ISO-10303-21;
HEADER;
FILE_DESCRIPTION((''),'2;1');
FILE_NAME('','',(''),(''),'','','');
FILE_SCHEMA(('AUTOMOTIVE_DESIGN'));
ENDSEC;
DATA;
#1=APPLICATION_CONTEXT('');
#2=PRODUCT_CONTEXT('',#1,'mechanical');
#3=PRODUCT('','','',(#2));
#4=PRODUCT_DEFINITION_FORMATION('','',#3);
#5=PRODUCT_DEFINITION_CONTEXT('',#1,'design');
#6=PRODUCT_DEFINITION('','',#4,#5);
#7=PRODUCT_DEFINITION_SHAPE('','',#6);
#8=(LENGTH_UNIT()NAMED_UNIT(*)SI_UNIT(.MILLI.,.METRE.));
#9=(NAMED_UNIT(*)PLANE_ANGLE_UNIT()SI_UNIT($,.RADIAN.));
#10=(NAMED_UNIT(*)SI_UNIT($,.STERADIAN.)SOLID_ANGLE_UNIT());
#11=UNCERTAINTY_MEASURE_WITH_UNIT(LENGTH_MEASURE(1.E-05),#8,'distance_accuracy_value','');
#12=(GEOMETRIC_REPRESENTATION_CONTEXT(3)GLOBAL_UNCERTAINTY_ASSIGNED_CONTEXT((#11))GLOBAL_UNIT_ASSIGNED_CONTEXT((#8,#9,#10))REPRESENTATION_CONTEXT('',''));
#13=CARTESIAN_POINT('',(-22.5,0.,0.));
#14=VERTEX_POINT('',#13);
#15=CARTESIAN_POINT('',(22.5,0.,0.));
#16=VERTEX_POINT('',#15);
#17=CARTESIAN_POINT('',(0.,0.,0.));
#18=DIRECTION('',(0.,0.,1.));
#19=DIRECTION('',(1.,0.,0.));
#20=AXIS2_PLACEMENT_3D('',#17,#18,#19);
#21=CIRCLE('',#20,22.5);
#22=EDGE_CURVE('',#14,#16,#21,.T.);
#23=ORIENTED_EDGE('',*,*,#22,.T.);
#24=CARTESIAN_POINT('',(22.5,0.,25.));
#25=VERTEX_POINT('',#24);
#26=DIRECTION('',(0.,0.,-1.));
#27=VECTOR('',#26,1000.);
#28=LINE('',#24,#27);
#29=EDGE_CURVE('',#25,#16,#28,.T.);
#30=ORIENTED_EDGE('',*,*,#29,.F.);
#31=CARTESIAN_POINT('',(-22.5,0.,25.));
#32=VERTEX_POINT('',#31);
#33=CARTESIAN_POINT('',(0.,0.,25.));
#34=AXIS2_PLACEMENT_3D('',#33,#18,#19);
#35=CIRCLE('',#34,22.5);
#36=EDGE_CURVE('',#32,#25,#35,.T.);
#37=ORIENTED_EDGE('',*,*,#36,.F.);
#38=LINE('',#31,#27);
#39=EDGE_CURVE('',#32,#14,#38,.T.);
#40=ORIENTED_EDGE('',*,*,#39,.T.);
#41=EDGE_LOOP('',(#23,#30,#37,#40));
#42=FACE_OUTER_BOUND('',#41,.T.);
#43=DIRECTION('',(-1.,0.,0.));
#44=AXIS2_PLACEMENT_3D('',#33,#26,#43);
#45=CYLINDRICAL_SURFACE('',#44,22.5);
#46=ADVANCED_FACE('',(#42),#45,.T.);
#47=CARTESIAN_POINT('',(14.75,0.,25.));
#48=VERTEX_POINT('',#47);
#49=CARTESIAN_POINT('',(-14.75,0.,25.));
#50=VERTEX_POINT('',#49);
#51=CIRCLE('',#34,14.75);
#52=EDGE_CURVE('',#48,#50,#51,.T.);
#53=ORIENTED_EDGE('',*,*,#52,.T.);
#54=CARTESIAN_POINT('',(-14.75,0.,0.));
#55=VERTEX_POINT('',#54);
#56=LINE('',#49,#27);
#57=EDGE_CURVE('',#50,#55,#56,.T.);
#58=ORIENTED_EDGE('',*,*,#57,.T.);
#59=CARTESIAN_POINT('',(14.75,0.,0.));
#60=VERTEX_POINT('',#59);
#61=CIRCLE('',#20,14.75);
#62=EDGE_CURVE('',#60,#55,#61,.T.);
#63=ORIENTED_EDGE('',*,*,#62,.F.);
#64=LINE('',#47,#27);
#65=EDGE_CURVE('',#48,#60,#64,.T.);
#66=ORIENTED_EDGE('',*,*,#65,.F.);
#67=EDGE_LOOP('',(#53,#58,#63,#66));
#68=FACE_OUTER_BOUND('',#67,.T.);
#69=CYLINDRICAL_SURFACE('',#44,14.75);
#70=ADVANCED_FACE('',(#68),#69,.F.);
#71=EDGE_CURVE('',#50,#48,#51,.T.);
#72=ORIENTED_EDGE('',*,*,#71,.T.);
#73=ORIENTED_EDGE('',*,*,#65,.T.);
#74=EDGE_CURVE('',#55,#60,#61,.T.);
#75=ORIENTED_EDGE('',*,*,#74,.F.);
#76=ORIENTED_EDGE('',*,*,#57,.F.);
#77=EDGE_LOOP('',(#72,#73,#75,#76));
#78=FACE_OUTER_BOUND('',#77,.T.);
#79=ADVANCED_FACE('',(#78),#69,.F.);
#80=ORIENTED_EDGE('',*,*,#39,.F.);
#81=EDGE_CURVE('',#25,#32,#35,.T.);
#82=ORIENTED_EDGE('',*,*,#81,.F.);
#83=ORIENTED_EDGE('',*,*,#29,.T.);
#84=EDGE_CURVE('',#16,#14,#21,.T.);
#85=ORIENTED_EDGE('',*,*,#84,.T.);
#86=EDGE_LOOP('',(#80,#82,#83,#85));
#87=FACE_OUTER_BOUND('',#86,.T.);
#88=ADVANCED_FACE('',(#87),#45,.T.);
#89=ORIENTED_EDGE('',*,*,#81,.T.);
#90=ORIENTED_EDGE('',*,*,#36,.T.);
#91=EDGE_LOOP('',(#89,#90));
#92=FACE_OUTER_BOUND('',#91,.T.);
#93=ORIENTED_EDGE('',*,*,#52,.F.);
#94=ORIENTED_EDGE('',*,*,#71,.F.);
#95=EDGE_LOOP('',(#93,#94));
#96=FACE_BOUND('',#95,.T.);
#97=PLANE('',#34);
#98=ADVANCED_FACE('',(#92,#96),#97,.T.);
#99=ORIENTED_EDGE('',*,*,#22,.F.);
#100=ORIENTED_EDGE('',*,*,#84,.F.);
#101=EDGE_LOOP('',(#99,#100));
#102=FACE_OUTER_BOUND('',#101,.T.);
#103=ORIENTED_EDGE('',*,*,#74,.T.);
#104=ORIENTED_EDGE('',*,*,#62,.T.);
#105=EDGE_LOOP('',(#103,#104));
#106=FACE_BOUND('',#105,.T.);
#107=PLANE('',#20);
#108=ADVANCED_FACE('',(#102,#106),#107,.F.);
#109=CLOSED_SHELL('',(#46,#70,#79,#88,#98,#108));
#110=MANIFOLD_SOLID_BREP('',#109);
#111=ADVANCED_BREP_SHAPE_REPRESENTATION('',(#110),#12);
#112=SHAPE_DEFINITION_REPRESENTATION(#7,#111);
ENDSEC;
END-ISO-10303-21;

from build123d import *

# Parameters (mm, degrees)
SKETCH1_R           = 22.5
SKETCH1_R_2         = 14.75
BOSS_EXTRUDE1_DEPTH = 25


with BuildPart() as part:
    # Sketch1 → Boss-Extrude1 (new body)
    with BuildSketch(Plane.XY):
        Circle(SKETCH1_R)
        Circle(SKETCH1_R_2, mode=Mode.SUBTRACT)
    extrude(amount=BOSS_EXTRUDE1_DEPTH)


solid = part.part
